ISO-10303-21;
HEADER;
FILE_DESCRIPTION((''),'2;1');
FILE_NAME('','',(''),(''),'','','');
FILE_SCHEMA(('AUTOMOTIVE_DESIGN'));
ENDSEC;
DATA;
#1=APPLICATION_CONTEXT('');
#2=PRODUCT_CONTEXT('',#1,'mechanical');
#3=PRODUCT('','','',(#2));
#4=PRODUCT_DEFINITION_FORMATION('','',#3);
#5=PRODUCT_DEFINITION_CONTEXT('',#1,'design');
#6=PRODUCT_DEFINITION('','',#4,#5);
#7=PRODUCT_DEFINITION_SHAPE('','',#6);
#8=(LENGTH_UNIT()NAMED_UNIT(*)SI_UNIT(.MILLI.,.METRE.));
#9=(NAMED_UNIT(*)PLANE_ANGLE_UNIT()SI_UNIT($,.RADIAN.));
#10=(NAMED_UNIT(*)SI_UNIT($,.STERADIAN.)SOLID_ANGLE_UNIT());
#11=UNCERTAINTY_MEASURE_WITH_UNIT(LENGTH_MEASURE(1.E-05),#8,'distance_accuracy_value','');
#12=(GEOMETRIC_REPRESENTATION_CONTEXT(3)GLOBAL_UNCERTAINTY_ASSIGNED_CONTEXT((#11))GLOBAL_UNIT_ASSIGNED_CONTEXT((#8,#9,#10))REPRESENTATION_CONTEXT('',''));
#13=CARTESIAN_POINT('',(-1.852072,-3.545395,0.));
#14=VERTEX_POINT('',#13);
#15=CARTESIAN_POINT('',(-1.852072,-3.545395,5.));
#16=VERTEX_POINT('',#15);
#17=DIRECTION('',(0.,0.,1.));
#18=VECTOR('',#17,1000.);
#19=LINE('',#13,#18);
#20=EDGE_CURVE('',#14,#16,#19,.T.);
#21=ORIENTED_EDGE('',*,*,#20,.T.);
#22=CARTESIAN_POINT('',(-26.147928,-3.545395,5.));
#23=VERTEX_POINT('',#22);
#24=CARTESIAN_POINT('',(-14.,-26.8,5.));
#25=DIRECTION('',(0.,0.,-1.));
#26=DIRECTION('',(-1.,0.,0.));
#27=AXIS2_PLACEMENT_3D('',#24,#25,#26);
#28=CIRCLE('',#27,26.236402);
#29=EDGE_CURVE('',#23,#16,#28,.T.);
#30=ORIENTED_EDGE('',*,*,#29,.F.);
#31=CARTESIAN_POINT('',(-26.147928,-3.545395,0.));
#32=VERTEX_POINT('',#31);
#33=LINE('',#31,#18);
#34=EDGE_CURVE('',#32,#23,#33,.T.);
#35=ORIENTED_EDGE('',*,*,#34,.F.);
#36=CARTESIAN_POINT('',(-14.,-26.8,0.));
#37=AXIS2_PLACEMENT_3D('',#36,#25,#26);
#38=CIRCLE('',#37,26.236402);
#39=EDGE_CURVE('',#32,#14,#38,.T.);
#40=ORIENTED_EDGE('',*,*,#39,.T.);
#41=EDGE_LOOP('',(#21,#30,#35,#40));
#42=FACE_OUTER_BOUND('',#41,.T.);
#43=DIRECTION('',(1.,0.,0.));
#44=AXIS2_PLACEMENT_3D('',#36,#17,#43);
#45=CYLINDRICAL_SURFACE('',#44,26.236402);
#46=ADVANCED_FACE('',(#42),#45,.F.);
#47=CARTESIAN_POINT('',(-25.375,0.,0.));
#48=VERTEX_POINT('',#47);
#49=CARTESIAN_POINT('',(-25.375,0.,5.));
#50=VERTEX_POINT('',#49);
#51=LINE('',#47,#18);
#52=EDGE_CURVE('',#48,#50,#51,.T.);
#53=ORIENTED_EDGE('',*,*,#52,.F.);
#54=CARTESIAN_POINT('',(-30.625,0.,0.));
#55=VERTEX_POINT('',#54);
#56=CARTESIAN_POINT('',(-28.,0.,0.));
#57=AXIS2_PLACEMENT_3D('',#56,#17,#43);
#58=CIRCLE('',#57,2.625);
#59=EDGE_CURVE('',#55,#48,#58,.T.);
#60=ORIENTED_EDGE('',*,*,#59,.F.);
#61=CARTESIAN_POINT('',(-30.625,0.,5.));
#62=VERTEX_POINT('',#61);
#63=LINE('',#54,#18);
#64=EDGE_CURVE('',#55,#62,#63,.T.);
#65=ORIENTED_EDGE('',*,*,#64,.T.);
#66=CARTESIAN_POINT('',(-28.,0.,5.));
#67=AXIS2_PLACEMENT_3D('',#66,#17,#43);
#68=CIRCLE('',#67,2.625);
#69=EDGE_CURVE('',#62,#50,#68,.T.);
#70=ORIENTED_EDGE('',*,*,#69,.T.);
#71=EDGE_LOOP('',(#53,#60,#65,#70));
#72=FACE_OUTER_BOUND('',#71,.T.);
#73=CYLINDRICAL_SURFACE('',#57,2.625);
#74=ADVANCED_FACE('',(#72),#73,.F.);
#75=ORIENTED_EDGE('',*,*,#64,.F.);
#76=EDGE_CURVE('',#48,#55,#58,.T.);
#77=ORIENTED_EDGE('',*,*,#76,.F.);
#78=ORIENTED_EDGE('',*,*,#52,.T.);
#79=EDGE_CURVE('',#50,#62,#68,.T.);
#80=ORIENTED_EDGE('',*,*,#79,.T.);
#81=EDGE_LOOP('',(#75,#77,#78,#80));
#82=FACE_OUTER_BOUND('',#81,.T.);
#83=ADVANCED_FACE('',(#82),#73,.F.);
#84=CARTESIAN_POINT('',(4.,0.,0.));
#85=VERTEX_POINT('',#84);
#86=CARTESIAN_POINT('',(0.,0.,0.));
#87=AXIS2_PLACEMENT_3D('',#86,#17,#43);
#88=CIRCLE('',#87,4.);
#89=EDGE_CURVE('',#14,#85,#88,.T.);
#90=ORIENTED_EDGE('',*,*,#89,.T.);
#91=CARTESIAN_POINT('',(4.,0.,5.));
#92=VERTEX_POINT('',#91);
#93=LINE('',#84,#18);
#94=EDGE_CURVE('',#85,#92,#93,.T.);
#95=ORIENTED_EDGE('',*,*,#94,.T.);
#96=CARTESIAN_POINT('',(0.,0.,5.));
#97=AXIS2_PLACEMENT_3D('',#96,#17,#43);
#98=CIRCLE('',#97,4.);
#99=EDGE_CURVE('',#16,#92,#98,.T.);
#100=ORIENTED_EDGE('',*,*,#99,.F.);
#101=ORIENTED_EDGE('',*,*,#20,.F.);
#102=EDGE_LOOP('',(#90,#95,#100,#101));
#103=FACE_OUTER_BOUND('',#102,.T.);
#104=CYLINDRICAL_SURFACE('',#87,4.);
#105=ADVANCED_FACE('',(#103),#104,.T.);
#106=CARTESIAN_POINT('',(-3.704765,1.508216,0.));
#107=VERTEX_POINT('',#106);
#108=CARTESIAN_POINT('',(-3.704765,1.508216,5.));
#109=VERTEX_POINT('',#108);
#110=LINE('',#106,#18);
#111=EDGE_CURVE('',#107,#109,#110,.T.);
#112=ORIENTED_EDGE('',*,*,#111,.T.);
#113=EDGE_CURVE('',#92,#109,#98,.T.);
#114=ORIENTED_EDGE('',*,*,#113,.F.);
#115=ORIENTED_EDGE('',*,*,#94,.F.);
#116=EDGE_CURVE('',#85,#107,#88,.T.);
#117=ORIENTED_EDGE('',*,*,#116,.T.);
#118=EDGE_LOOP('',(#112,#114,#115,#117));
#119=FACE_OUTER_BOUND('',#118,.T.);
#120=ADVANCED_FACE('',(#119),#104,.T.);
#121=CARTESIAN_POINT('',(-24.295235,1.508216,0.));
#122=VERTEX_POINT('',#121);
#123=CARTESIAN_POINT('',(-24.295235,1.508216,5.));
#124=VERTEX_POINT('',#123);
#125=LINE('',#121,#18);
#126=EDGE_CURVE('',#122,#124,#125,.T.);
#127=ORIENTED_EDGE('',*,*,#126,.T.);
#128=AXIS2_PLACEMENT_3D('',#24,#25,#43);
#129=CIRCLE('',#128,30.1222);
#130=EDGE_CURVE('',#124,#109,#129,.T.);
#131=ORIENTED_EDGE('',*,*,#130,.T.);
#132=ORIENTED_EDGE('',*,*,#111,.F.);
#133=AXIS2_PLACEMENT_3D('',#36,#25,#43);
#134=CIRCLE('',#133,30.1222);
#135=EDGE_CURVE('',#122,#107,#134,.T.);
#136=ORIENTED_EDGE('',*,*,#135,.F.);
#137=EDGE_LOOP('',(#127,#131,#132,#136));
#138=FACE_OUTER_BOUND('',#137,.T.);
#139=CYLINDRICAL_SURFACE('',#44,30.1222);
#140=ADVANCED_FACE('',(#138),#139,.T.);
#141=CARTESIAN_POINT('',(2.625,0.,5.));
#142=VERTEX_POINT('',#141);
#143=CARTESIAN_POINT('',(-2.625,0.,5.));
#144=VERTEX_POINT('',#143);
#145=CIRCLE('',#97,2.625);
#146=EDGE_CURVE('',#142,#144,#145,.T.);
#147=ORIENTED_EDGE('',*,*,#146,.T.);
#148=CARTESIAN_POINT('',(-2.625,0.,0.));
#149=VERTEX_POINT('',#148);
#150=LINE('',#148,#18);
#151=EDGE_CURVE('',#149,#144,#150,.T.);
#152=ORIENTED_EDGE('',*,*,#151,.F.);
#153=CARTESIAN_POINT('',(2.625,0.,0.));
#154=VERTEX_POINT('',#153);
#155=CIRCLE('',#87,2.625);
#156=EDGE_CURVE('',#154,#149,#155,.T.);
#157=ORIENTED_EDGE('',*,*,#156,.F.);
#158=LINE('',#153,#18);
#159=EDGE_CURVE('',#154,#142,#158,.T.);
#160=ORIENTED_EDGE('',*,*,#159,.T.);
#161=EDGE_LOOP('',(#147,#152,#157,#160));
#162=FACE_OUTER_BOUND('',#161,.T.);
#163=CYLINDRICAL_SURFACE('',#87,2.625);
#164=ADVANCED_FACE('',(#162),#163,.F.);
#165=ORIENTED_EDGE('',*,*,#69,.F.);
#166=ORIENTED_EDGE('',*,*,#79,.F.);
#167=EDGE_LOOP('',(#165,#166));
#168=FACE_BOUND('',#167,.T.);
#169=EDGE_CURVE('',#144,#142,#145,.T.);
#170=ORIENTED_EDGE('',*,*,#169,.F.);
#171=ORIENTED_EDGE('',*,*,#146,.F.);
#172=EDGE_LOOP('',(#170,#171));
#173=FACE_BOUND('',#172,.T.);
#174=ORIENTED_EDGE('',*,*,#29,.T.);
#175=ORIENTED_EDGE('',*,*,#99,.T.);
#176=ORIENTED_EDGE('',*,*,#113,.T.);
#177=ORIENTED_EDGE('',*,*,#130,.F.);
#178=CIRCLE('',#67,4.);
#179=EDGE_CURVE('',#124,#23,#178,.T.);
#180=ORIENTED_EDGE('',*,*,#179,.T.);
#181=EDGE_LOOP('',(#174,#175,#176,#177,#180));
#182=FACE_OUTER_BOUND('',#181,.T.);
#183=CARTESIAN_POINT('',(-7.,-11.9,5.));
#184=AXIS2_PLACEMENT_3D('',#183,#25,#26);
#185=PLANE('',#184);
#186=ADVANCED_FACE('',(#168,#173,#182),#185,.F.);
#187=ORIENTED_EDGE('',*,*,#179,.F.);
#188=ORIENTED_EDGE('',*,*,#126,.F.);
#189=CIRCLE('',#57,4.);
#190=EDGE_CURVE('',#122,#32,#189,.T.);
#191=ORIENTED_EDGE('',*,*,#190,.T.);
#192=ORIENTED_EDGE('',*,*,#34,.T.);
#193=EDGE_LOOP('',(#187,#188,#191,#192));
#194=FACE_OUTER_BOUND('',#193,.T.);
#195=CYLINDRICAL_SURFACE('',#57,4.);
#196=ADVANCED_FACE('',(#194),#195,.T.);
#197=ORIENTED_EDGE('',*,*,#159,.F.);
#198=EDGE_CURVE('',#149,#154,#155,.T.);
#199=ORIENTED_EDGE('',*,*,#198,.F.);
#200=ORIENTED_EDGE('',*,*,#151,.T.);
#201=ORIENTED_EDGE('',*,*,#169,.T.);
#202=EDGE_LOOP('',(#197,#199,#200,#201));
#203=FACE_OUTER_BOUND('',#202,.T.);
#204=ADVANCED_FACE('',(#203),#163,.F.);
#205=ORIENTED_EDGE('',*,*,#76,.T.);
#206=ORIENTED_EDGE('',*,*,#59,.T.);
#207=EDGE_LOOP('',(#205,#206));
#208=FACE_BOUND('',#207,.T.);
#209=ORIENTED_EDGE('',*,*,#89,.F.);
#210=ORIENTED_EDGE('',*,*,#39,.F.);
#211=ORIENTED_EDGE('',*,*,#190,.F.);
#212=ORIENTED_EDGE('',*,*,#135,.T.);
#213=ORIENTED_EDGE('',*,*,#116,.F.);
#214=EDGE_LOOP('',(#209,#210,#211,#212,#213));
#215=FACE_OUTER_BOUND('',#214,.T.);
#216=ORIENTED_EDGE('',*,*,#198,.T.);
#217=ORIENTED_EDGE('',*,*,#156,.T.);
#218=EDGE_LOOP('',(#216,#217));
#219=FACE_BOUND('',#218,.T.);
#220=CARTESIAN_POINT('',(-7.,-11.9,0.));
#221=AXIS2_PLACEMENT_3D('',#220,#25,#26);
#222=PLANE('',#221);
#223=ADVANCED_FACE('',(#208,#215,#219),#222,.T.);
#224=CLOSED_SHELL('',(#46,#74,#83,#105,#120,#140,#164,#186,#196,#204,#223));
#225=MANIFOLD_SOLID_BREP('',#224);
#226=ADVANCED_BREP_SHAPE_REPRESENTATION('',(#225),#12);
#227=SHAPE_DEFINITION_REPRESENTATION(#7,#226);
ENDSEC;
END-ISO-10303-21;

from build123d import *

# Parameters (mm, degrees)
BOSS_EXTRUDE1_DEPTH = 5
SKETCH2_R           = 1.5
CUT_EXTRUDE1_DEPTH  = 3
BOSS_EXTRUDE2_DEPTH = 5
SKETCH4_R           = 2.625
CUT_EXTRUDE2_DEPTH  = 34.097061453
CUT_EXTRUDE3_DEPTH  = 34.097061453
BOSS_EXTRUDE3_DEPTH = 5


with BuildPart() as part:
    # Sketch1 → Boss-Extrude1 (new body)
    with BuildSketch(Plane.XY):
        with BuildLine():
            ThreePointArc((-26.738194812, 2.158204732), (-30.234084304, -1.121992567), (-25.515357454, -0.276679267))
            ThreePointArc((-25.515357454, -0.276679267), (-19.880574881, 1.510931441), (-14, 2.115220905))
            ThreePointArc((-14, 2.115220905), (-8.119425119, 1.510931441), (-2.484642546, -0.276679267))
            ThreePointArc((-2.484642546, -0.276679267), (2.234084304, -1.121992567), (-1.261805188, 2.158204732))
            ThreePointArc((-1.261805188, 2.158204732), (-7.461545448, 4.366267273), (-14, 5.115220905))
            ThreePointArc((-14, 5.115220905), (-20.538454552, 4.366267273), (-26.738194812, 2.158204732))
        make_face()
    extrude(amount=BOSS_EXTRUDE1_DEPTH)

    # Sketch2 → Cut-Extrude1 (cut)
    with BuildSketch(Plane.XY.offset(5)):
        with Locations((-28, 0)):
            Circle(SKETCH2_R)
        Circle(SKETCH2_R)
    extrude(amount=-CUT_EXTRUDE1_DEPTH, mode=Mode.SUBTRACT)

    # Sketch3 → Boss-Extrude2 (add, through all)
    with BuildSketch(Plane.XY.offset(5)):
        with BuildLine():
            ThreePointArc((-27.059016708, 3.887743619), (-31.451726366, -2.021283032), (-24.149017572, -1.081635031))
            ThreePointArc((-24.149017572, -1.081635031), (-14, 0.848451211), (-3.850982428, -1.081635031))
            ThreePointArc((-3.850982428, -1.081635031), (3.451726366, -2.021283032), (-0.940983292, 3.887743619))
            ThreePointArc((-0.940983292, 3.887743619), (-13.167819997, 6.801577419), (-25.534946827, 4.556552431))
            ThreePointArc((-25.534946827, 4.556552431), (-26.301527828, 4.232507508), (-27.059016708, 3.887743619))
        make_face()
    extrude(amount=-BOSS_EXTRUDE2_DEPTH)

    # Sketch4 → Cut-Extrude2 (cut, through all)
    with BuildSketch(Plane.XY.offset(5)):
        with Locations((-28, 0)):
            Circle(SKETCH4_R)
        Circle(SKETCH4_R)
    extrude(amount=-CUT_EXTRUDE2_DEPTH, mode=Mode.SUBTRACT)

    # Sketch5 → Cut-Extrude3 (cut, through all)
    with BuildSketch(Plane.XY.offset(5)):
        with BuildLine():
            Line((-14.205977149, 10.740702715), (-0.940983292, 3.887743619))
            ThreePointArc((-0.940983292, 3.887743619), (-14, 6.812890489), (-27.059016708, 3.887743619))
            Line((-27.059016708, 3.887743619), (-14.205977149, 10.740702715))
        make_face()
        with BuildLine():
            ThreePointArc((-0.940983292, 3.887743619), (-14, 6.812890489), (-27.059016708, 3.887743619))
            ThreePointArc((-27.059016708, 3.887743619), (-25.390156506, 3.031289649), (-24.295234779, 1.50821572))
            ThreePointArc((-24.295234779, 1.50821572), (-14, 3.322200059), (-3.704765221, 1.50821572))
            ThreePointArc((-3.704765221, 1.50821572), (-2.609843494, 3.031289649), (-0.940983292, 3.887743619))
        make_face()
    extrude(amount=-CUT_EXTRUDE3_DEPTH, mode=Mode.SUBTRACT)

    # Sketch7 → Boss-Extrude3 (add, through all)
    with BuildSketch(Plane.XY.offset(5)):
        with BuildLine():
            Line((-26.14792778, -3.545395393), (-24.177787081, 0.278127161))
            Line((-24.177787081, 0.278127161), (-14.756553685, 2.142998553))
            Line((-14.756553685, 2.142998553), (-4.34233682, 0.278127161))
            Line((-4.34233682, 0.278127161), (-2.53651725, -2.31550038))
            Line((-2.53651725, -2.31550038), (-1.85207222, -3.545395393))
            ThreePointArc((-1.85207222, -3.545395393), (-14, -0.563598098), (-26.14792778, -3.545395393))
        make_face()
    extrude(amount=-BOSS_EXTRUDE3_DEPTH)


solid = part.part
